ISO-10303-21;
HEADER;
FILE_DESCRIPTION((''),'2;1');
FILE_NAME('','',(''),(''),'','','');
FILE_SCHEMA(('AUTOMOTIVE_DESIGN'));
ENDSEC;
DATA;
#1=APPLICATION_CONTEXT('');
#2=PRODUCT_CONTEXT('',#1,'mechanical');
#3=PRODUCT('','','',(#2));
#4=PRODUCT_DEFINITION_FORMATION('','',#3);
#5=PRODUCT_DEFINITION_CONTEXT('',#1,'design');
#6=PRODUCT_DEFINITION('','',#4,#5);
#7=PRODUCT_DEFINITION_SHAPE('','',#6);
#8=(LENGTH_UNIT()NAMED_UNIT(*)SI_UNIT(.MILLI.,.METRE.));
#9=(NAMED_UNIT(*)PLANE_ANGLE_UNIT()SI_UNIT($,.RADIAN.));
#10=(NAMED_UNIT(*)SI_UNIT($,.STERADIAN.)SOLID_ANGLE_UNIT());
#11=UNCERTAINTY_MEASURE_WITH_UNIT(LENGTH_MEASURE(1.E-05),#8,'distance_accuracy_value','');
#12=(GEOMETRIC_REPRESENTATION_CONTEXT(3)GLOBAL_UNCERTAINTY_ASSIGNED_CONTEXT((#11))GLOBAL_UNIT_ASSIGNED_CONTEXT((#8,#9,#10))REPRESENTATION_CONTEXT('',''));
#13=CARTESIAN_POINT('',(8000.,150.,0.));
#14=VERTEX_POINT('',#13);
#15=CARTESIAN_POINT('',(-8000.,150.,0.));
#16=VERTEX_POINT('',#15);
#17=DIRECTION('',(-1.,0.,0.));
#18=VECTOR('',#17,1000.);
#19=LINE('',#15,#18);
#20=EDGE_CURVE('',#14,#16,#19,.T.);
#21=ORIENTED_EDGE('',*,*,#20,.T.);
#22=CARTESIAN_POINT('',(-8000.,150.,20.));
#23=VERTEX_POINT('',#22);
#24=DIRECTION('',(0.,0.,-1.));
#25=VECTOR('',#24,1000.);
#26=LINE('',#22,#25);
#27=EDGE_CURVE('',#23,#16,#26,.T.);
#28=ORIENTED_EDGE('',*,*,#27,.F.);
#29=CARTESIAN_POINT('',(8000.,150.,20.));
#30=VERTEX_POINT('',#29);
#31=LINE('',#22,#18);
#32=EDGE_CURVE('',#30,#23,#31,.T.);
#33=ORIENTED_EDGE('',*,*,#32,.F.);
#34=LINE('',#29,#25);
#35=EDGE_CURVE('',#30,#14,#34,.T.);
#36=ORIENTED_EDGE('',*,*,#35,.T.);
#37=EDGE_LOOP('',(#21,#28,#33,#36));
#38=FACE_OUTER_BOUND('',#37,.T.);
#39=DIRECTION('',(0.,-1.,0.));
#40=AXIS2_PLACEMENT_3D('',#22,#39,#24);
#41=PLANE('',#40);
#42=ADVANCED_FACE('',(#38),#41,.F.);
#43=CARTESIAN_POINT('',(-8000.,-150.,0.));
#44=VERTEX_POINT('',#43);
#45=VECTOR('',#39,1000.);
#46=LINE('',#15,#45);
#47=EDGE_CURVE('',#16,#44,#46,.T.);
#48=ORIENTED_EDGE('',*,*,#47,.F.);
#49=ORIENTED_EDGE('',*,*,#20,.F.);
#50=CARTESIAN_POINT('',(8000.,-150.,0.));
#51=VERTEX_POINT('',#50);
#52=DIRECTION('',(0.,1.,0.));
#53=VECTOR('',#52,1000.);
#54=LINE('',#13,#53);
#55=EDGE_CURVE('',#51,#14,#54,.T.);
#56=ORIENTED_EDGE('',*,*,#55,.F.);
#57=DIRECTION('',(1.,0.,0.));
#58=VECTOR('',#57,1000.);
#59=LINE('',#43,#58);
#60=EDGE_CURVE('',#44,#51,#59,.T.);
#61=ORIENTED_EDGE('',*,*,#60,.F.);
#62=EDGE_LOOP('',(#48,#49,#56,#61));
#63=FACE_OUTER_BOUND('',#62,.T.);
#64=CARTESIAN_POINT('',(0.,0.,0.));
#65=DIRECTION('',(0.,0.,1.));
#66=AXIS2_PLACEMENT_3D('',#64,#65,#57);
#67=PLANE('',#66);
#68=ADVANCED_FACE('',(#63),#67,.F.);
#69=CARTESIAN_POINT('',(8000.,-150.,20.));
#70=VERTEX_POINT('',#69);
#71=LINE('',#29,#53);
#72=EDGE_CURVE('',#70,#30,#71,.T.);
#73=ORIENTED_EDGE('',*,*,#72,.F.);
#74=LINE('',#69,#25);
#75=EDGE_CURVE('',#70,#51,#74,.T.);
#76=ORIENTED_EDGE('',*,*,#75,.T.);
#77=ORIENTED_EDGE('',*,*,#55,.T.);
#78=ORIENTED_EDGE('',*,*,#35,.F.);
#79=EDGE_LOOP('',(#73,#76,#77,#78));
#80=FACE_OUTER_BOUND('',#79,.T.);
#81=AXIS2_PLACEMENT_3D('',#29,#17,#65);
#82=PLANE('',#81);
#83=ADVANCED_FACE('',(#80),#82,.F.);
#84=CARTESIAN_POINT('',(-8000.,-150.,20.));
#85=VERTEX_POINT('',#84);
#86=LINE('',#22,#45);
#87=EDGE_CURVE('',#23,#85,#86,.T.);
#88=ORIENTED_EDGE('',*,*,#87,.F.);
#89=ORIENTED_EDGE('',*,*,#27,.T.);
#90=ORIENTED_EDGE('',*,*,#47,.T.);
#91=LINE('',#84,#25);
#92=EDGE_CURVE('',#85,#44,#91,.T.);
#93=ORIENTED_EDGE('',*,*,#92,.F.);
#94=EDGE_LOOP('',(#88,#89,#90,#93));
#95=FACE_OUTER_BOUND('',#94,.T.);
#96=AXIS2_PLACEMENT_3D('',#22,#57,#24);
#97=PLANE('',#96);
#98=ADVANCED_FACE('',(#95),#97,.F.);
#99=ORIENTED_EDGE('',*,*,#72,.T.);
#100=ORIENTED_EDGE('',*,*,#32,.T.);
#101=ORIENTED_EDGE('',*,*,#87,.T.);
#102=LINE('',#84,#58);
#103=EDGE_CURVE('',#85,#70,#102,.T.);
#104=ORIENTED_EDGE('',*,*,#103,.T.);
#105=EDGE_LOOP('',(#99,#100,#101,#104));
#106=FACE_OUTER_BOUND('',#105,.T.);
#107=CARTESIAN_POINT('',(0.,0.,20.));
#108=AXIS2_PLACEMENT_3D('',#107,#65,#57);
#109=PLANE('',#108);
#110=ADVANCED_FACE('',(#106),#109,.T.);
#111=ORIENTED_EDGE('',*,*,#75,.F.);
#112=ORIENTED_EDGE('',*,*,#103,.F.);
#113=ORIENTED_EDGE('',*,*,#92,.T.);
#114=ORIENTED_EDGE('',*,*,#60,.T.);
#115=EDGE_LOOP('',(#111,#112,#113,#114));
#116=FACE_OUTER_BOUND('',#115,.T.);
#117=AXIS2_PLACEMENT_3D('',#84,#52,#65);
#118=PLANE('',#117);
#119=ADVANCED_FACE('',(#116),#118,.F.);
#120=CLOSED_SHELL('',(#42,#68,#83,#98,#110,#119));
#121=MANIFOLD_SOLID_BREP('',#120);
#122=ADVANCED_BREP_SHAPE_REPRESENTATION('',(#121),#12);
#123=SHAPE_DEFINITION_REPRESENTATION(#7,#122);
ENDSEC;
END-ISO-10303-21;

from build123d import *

# Parameters (mm, degrees)
SKETCH1_W           = 16000
SKETCH1_H           = 300
BOSS_EXTRUDE1_DEPTH = 20


with BuildPart() as part:
    # Sketch1 → Boss-Extrude1 (new body)
    with BuildSketch(Plane.XY):
        Rectangle(SKETCH1_W, SKETCH1_H)
    extrude(amount=BOSS_EXTRUDE1_DEPTH)


solid = part.part
